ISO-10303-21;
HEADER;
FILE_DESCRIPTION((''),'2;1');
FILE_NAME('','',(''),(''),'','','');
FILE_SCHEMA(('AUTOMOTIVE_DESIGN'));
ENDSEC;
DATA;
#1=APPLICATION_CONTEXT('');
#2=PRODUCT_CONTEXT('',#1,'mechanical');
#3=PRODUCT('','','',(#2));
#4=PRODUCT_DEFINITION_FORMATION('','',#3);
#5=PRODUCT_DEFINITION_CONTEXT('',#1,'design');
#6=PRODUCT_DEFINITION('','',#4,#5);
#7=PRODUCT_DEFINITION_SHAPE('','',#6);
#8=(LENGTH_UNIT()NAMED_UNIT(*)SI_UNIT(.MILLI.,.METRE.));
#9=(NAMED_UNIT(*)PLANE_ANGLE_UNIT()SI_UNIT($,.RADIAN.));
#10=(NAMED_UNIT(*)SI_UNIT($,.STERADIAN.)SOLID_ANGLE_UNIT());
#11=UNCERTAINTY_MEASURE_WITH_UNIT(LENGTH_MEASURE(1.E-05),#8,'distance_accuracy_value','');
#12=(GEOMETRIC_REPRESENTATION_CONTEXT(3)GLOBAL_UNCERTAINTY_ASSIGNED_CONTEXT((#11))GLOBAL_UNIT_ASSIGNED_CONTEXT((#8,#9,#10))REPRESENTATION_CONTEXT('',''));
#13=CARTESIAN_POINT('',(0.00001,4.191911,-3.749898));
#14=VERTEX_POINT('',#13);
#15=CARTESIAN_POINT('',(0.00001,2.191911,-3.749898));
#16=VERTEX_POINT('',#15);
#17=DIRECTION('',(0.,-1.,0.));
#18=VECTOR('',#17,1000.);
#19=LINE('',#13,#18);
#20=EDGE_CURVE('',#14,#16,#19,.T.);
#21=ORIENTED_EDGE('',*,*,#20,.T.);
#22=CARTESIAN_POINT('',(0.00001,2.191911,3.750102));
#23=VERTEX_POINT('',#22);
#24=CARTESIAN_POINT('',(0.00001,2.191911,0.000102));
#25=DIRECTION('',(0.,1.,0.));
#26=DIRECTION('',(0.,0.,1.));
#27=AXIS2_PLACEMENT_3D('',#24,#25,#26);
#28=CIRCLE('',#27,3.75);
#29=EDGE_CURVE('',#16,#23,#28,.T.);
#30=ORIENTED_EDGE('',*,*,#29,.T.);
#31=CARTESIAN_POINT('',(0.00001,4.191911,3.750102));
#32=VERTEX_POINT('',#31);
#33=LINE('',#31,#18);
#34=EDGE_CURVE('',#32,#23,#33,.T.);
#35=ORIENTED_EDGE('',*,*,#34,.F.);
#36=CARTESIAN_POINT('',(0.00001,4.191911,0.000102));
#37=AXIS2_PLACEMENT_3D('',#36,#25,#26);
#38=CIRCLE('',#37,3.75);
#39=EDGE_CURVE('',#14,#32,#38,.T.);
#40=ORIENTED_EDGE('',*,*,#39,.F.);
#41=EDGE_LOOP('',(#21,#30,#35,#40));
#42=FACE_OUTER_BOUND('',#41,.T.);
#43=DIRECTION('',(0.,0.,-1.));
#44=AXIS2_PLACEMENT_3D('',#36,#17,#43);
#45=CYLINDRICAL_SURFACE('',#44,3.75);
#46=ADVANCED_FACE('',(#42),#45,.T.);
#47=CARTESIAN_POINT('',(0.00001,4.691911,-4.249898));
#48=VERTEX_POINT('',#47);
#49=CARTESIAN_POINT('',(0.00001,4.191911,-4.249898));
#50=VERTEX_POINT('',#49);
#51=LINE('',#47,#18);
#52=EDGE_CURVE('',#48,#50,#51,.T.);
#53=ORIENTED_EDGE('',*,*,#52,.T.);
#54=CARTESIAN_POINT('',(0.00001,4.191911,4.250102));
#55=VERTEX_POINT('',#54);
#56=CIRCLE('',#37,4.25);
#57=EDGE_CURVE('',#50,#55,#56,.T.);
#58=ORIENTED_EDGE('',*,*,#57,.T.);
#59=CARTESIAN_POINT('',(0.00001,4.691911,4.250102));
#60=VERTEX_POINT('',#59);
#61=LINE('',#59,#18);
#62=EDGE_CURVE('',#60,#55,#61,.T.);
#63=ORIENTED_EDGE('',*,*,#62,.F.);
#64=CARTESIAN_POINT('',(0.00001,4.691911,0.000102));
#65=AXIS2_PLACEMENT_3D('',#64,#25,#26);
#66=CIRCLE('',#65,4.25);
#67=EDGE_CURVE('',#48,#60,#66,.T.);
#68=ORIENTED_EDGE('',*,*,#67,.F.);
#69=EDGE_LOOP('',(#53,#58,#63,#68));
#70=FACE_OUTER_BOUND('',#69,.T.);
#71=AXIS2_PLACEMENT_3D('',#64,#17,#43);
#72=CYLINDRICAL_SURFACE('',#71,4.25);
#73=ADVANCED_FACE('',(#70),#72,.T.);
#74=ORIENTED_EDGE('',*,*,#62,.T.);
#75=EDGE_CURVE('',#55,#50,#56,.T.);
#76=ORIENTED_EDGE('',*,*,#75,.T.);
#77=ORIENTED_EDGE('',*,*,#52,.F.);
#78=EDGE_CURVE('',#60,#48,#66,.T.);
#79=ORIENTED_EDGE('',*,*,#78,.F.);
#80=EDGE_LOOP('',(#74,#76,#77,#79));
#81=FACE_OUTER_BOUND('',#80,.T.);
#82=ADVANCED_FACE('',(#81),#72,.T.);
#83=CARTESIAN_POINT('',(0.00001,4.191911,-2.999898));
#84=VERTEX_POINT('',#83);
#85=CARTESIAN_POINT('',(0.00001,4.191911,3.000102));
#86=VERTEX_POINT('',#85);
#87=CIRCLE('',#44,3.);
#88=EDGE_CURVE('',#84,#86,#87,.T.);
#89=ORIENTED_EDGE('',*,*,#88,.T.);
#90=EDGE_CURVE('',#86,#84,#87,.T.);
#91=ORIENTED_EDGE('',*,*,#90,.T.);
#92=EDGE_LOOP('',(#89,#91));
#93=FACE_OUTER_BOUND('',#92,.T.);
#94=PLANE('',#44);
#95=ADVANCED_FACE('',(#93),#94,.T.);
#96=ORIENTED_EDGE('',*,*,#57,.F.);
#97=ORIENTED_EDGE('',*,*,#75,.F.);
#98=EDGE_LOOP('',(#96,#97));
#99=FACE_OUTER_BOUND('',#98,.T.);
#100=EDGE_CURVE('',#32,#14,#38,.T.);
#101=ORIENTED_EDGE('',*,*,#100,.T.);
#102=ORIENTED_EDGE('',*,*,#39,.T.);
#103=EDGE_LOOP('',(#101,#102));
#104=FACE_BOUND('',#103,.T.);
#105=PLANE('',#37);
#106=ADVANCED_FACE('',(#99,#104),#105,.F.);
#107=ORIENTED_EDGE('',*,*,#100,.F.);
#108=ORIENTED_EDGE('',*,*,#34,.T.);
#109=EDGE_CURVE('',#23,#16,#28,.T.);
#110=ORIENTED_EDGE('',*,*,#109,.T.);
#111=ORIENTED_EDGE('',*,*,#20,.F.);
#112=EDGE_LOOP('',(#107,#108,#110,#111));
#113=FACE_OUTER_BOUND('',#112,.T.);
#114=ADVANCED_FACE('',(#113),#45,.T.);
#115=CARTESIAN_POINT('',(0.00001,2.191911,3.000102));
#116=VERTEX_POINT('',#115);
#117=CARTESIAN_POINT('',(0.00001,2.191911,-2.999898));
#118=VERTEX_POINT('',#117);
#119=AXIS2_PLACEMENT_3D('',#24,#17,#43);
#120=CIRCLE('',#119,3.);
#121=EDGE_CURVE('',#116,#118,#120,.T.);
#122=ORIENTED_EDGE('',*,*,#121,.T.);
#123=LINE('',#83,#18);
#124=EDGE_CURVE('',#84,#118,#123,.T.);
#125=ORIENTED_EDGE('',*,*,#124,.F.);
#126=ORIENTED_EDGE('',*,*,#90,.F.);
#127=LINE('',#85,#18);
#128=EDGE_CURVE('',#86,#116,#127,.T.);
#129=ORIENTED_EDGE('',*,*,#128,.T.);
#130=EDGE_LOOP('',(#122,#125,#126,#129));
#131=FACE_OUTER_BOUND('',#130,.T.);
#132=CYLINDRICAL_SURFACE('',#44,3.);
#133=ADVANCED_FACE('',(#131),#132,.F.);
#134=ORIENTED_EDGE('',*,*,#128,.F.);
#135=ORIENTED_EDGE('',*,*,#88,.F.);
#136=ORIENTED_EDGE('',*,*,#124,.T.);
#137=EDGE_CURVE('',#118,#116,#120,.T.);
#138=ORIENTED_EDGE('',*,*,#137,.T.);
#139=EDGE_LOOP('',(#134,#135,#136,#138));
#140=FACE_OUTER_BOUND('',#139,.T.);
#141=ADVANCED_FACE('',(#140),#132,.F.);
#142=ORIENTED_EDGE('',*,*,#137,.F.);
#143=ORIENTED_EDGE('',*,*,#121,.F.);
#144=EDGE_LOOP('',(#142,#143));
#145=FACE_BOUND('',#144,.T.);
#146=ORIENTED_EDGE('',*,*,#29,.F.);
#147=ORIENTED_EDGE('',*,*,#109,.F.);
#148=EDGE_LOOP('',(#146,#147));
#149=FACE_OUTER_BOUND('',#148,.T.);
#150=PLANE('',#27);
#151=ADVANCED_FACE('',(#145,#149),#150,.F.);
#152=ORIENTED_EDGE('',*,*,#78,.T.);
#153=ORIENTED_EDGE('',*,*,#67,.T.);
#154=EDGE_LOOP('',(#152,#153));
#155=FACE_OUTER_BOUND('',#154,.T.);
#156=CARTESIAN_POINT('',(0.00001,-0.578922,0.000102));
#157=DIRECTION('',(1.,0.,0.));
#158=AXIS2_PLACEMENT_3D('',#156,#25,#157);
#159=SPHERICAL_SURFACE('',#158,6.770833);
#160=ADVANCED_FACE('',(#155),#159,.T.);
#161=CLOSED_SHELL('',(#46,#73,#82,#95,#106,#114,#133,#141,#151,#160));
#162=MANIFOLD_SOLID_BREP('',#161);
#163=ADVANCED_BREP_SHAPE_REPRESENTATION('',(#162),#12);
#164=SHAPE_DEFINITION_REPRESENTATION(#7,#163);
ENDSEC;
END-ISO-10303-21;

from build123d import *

# Parameters (mm, degrees)
SKETCH1_R           = 7.5
BOSS_EXTRUDE1_DEPTH = 4
SKETCH2_R           = 8.5
BOSS_EXTRUDE2_DEPTH = 1
DOME1_FACE_RADIUS   = 8.5
DOME1_HEIGHT        = 3
SKETCH3_R           = 6
CUT_EXTRUDE1_DEPTH  = 4
SCALE1_SCALE        = 0.5


with BuildPart() as part:
    # Sketch1 → Boss-Extrude1 (new body)
    with BuildSketch(Plane(origin=(0, 0, 0), x_dir=(1, 0, 0), z_dir=(0, 1, 0))):
        with Locations(Location((0, 0, 0), (0, 0, 270))):
            Circle(SKETCH1_R)
    extrude(amount=BOSS_EXTRUDE1_DEPTH)

    # Sketch2 → Boss-Extrude2 (add)
    with BuildSketch(Plane(origin=(0, 4, 0), x_dir=(1, 0, 0), z_dir=(0, 1, 0))):
        with Locations(Location((0, 0, 0), (0, 0, 270))):
            Circle(SKETCH2_R)
    extrude(amount=BOSS_EXTRUDE2_DEPTH)

    # Dome1: a dome of height H over a round flat face of radius A is a cap of a sphere of radius (A * A + H * H) / (2 * H)
    dome1_r = (DOME1_FACE_RADIUS * DOME1_FACE_RADIUS + DOME1_HEIGHT * DOME1_HEIGHT) / (2 * DOME1_HEIGHT)
    dome1_base = Plane((0, 5, 0), z_dir=(0, 1, 0))
    with Locations(dome1_base.offset(DOME1_HEIGHT - dome1_r)):
        dome1_ball = Sphere(dome1_r, mode=Mode.PRIVATE)
    add(split(dome1_ball, bisect_by=dome1_base, keep=Keep.TOP, mode=Mode.PRIVATE))

    # Sketch3 → Cut-Extrude1 (cut)
    with BuildSketch(Plane.XZ):
        with Locations(Location((0, 0, 0), (0, 0, 270))):
            Circle(SKETCH3_R)
    extrude(amount=-CUT_EXTRUDE1_DEPTH, mode=Mode.SUBTRACT)


with BuildPart() as part_1:
    # Scale1: scaled about (0, 4.383748239, 0)
    add(part.part.scale(SCALE1_SCALE).moved(Location((0, 2.191874119, 0))))


solid = part_1.part
